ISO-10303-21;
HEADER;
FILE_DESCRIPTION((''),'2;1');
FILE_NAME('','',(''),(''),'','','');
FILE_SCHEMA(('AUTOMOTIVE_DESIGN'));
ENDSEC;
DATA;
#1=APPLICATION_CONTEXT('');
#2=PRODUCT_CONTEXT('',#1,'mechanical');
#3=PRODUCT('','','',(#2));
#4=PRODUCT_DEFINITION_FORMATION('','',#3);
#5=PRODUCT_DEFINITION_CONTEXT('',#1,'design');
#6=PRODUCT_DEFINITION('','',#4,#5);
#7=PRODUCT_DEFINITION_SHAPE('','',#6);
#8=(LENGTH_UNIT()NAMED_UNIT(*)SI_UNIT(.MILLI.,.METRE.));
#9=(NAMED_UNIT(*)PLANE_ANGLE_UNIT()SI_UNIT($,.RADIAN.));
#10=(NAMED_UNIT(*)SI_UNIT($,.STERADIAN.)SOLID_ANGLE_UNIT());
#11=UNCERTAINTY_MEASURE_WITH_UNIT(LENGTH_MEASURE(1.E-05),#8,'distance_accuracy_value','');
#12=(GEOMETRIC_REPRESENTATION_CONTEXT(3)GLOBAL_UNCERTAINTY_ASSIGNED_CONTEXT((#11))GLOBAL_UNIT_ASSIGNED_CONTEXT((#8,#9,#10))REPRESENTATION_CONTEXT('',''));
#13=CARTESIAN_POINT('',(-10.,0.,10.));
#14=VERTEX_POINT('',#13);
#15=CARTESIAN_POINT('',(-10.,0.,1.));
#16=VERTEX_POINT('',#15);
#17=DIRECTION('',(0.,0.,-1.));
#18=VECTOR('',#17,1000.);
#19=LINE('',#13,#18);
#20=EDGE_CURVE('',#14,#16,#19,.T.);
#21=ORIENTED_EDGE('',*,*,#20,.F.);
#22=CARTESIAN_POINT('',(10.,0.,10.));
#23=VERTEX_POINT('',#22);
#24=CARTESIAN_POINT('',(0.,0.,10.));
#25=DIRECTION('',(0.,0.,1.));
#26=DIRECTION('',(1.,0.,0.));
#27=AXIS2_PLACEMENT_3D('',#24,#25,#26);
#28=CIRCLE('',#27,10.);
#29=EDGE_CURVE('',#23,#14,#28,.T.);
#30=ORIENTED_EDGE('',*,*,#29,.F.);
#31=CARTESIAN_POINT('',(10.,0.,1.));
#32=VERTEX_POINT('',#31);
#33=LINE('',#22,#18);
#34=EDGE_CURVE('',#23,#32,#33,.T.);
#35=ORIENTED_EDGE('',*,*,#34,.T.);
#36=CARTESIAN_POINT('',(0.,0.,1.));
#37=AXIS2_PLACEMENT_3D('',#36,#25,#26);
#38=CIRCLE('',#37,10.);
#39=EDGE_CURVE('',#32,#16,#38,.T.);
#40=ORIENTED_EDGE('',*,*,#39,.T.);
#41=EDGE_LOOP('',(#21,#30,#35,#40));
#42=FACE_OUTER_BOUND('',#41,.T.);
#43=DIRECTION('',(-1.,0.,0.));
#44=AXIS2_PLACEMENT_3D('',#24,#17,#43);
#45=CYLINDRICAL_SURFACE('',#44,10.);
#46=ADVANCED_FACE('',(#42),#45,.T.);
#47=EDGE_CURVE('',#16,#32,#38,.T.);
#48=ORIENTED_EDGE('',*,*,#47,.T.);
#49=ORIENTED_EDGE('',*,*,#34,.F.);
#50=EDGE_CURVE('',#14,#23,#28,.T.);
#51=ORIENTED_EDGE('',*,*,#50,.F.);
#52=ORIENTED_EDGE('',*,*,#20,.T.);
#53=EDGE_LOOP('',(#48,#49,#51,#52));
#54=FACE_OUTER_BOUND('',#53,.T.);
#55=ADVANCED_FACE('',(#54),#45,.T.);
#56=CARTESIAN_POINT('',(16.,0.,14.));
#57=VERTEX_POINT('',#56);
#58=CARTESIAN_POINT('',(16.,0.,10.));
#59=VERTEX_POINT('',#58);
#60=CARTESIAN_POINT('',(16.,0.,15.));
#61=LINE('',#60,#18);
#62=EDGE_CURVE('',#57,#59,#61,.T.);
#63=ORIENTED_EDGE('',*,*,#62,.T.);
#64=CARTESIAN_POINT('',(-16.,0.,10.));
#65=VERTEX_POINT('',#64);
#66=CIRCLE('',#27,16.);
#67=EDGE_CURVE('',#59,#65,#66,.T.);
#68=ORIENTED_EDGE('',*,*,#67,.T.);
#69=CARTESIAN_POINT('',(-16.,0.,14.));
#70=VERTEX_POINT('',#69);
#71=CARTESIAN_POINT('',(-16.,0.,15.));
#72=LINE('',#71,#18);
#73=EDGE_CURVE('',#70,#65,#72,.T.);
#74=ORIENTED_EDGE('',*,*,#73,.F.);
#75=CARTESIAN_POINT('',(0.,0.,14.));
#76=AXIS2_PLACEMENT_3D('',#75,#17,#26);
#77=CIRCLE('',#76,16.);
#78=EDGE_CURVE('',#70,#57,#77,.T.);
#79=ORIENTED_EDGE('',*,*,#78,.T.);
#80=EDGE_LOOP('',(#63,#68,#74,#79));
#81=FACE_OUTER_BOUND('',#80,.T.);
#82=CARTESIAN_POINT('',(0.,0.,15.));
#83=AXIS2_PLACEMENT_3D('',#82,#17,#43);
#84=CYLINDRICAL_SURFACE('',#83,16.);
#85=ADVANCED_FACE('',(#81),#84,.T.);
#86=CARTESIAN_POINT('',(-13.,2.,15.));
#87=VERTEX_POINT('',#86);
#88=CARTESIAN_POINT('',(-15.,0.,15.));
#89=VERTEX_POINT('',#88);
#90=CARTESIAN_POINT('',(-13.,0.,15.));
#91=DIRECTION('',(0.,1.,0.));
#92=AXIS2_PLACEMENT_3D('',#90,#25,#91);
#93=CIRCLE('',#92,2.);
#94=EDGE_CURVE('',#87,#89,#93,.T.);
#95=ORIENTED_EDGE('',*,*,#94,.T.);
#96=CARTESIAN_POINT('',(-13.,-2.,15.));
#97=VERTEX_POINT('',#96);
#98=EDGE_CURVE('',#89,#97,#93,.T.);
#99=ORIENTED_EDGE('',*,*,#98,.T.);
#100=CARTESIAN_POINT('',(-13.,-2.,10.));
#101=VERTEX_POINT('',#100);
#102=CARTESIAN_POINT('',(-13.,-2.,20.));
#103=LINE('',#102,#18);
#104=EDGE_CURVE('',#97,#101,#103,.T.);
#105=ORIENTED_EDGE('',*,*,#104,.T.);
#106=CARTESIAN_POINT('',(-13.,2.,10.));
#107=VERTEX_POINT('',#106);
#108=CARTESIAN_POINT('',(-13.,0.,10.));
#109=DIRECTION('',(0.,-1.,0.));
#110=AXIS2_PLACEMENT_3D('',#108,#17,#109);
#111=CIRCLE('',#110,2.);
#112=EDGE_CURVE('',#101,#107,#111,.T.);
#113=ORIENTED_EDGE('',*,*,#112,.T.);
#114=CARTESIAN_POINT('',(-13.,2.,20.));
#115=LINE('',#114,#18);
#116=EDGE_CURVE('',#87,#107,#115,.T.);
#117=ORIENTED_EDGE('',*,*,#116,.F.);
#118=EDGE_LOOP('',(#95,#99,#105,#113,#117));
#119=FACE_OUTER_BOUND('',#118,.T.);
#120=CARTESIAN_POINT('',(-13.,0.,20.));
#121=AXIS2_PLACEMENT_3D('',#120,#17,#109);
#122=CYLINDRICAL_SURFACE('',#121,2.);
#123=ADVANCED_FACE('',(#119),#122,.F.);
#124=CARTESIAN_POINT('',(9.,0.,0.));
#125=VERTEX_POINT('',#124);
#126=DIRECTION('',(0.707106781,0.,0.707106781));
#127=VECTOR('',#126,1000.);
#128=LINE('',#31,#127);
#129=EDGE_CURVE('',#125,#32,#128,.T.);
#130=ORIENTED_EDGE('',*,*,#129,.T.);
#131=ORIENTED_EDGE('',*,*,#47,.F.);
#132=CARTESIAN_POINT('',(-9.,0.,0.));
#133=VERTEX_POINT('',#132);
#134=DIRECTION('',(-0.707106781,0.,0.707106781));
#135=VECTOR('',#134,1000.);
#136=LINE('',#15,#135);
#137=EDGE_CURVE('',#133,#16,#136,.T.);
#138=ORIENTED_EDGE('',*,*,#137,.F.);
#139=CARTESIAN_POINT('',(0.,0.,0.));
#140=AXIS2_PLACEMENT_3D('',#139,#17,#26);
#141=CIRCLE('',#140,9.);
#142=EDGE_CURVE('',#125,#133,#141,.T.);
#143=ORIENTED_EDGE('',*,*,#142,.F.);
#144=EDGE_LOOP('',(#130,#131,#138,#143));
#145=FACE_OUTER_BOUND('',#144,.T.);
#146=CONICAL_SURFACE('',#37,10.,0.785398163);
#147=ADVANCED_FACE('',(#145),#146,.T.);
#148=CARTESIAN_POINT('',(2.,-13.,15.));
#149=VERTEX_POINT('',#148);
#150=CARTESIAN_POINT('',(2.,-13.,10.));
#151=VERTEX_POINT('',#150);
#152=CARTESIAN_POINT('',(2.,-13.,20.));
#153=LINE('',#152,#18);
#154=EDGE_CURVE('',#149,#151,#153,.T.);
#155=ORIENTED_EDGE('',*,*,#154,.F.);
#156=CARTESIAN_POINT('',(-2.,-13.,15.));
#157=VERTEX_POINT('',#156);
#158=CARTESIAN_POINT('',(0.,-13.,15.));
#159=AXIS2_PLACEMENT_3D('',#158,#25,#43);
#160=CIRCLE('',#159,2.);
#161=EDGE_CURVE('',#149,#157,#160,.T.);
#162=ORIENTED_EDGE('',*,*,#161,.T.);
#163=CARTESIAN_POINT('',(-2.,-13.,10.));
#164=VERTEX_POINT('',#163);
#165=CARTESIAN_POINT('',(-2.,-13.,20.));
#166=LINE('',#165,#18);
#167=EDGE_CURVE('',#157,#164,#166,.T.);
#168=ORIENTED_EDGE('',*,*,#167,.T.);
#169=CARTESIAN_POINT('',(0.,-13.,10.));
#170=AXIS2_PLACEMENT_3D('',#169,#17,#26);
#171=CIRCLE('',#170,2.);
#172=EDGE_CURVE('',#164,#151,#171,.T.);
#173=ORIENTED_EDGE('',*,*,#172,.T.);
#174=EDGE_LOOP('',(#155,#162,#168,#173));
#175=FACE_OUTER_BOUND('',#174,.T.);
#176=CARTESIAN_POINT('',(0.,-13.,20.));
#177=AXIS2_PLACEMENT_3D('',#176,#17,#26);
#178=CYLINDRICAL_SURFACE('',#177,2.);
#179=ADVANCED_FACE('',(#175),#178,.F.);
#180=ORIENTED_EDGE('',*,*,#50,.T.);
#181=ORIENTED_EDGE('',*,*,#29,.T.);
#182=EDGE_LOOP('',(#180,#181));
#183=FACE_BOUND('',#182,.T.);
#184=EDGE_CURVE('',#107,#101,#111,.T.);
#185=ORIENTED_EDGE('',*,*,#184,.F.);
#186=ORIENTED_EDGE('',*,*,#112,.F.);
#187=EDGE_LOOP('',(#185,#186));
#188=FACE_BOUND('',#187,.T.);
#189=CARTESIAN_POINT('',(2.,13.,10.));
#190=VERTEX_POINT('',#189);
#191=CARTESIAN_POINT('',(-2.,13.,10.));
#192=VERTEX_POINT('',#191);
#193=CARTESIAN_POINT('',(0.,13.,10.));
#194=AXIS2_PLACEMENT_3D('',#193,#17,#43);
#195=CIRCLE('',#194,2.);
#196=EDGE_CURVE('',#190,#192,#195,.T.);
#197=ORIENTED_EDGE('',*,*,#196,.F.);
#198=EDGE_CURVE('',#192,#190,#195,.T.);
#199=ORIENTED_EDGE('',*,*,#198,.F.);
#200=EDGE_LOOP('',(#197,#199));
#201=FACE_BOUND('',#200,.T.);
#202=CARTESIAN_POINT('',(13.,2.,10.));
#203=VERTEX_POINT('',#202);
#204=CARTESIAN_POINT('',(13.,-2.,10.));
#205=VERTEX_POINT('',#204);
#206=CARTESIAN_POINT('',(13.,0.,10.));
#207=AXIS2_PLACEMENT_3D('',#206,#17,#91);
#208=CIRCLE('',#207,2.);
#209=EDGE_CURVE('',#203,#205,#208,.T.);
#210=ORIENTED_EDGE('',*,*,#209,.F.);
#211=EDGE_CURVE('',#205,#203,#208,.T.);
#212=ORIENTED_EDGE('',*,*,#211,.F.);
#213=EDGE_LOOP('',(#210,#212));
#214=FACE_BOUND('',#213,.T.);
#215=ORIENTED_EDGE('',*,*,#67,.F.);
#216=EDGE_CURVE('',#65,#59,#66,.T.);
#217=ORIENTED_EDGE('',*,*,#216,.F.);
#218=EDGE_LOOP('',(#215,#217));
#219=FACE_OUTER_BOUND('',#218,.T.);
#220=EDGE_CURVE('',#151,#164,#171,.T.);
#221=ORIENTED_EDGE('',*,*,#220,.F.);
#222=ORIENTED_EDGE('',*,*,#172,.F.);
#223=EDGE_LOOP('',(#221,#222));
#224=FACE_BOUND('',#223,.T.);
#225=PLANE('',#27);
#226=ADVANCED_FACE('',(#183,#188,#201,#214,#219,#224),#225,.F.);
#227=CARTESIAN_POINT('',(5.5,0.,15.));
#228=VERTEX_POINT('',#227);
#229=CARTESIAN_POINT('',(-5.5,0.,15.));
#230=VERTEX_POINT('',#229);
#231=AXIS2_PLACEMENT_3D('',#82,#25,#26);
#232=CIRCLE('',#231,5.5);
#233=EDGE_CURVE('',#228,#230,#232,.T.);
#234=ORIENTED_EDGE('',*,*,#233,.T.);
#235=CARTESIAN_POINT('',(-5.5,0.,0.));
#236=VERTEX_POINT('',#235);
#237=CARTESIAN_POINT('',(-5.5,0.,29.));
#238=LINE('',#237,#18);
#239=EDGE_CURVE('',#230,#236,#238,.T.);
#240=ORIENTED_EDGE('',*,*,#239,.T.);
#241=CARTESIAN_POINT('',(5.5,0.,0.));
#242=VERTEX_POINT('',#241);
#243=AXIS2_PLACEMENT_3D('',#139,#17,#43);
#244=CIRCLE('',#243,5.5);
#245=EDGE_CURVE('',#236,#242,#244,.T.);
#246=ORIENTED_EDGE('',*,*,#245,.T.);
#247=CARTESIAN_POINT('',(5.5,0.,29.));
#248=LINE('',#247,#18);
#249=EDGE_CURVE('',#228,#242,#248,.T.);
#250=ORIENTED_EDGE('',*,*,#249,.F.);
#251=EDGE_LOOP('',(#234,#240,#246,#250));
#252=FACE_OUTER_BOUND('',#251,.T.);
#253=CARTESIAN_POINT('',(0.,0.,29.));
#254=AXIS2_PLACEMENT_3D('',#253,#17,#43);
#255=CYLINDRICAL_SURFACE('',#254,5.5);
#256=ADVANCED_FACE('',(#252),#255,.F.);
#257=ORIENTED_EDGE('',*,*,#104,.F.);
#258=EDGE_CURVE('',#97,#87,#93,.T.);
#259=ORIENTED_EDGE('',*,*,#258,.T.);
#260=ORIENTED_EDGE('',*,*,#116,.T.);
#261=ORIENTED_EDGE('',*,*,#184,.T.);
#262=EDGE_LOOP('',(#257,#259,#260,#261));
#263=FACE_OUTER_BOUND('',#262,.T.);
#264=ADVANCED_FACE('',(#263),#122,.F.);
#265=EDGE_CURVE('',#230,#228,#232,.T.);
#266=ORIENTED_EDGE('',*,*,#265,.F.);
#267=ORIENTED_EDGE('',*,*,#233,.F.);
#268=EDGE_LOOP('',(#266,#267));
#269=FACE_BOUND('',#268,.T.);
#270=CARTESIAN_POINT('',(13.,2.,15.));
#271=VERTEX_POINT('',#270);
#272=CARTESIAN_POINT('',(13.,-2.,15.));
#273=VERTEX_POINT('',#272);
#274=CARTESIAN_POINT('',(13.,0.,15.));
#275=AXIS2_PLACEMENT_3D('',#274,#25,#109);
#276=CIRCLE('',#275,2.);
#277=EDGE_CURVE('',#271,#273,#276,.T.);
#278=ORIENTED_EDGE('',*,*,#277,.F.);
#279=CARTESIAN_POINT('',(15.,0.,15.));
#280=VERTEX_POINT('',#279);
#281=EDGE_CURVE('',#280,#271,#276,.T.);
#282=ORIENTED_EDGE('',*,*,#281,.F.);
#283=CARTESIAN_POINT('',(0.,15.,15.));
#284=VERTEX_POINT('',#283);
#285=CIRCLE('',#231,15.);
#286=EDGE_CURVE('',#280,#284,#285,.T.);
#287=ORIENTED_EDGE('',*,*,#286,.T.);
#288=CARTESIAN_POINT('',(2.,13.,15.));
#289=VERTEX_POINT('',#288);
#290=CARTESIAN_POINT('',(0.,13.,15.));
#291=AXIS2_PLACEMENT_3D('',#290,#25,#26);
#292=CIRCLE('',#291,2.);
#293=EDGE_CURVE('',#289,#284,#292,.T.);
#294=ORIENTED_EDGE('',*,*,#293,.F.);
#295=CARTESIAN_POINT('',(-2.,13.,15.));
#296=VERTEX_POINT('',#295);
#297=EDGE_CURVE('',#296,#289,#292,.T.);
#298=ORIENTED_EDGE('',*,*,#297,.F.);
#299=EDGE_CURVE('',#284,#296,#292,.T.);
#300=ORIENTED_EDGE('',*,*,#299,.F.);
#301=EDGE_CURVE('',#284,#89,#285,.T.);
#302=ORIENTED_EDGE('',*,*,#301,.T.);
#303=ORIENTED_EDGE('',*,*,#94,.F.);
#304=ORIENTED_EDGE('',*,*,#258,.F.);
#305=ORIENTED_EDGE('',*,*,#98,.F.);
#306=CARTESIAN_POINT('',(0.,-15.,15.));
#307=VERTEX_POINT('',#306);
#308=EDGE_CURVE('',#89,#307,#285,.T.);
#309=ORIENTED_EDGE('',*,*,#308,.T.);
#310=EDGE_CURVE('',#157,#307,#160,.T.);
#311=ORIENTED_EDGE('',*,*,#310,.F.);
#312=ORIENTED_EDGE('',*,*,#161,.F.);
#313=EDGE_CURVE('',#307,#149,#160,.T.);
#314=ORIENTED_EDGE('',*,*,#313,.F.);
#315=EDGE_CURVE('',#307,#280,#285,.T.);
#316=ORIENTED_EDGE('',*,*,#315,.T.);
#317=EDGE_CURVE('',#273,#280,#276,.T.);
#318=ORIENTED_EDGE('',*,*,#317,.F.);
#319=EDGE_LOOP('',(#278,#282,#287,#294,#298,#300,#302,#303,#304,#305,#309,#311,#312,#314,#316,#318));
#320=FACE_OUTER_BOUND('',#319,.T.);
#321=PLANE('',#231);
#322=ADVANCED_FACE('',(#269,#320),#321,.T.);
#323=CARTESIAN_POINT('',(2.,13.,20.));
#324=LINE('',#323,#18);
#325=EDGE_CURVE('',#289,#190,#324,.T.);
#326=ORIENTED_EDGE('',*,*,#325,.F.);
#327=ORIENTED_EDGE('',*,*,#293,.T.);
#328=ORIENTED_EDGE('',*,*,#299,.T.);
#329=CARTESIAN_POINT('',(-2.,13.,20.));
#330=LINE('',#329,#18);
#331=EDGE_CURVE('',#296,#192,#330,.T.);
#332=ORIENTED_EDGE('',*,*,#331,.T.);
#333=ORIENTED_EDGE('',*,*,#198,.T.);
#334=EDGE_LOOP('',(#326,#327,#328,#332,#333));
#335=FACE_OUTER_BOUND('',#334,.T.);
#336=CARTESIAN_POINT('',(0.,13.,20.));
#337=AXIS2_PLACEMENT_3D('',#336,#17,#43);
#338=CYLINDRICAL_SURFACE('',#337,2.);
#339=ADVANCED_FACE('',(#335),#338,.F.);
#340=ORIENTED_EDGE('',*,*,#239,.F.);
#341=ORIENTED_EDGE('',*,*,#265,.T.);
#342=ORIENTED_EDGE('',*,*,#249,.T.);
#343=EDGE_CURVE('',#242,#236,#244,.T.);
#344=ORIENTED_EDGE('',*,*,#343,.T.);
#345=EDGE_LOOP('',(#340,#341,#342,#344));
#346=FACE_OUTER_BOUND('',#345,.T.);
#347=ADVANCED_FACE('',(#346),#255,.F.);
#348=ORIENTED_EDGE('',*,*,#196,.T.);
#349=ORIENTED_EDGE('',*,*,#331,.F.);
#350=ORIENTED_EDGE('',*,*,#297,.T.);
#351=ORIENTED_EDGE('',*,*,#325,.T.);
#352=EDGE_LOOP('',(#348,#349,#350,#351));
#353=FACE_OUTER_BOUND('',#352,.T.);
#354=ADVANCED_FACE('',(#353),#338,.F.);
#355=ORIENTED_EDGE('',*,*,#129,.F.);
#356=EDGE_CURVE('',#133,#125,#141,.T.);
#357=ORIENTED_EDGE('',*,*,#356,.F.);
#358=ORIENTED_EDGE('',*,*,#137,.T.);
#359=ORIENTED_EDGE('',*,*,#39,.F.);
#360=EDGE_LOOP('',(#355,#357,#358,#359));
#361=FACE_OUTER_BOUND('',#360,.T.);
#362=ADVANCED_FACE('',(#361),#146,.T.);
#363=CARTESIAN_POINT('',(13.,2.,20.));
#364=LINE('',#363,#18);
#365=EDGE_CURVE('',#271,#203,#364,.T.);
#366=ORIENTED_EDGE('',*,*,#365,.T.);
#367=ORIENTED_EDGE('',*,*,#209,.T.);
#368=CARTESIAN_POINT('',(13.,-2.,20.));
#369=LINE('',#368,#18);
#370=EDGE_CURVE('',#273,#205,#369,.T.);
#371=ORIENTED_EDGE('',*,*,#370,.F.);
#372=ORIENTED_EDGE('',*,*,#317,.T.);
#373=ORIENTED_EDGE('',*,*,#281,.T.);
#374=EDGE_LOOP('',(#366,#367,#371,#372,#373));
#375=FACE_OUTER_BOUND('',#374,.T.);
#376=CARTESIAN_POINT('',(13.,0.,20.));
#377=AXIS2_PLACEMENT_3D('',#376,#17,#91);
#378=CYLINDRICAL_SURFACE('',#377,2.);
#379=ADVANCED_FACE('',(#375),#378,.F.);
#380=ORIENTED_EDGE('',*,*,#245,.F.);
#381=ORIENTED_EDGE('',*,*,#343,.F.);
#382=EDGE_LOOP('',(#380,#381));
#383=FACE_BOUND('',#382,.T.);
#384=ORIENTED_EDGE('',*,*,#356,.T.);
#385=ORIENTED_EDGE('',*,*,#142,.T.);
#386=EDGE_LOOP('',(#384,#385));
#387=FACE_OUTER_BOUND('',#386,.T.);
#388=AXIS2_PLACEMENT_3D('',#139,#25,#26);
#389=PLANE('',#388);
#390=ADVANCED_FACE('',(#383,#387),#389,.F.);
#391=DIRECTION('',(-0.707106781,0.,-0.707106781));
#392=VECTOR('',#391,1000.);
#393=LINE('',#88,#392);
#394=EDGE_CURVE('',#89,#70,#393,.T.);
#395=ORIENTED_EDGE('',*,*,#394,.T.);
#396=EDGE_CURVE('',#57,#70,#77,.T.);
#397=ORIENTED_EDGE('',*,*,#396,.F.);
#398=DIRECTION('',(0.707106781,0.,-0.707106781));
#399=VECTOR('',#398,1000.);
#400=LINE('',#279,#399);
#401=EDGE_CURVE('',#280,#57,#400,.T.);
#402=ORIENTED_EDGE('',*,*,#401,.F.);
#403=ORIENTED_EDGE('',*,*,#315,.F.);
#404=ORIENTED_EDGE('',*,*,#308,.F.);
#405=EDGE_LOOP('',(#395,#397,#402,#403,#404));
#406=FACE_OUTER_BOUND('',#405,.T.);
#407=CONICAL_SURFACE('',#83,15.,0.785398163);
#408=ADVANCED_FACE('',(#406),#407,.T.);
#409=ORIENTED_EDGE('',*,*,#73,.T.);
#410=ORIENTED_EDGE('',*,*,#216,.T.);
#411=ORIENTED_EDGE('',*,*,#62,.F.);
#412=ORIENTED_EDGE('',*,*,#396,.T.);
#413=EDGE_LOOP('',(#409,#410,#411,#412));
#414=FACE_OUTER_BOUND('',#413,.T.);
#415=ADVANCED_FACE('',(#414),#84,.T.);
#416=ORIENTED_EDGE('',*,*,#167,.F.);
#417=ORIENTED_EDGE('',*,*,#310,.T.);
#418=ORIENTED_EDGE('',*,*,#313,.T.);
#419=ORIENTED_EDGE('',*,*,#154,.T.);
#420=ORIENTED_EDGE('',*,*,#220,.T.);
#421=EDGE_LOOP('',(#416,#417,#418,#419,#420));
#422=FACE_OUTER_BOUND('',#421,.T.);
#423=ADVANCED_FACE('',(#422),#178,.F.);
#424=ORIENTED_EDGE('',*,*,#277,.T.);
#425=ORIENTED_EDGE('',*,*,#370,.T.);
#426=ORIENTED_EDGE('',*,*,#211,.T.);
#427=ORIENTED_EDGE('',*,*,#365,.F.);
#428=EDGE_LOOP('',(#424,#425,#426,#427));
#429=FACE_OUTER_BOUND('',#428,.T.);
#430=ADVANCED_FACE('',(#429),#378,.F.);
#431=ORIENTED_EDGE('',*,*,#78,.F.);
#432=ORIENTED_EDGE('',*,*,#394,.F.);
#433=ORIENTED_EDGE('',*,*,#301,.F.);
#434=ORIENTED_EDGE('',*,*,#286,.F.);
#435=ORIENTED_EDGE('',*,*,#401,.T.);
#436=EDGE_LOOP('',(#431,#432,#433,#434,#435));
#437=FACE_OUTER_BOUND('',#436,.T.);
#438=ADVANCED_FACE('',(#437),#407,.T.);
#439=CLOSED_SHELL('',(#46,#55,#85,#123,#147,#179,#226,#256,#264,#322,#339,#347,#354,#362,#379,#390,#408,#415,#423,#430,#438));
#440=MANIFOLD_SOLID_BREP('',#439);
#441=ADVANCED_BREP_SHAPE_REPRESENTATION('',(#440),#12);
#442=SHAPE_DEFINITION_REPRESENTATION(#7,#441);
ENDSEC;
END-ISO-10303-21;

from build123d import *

# Parameters (mm, degrees)
SKETCH1_R           = 10
BOSS_EXTRUDE1_DEPTH = 10
SKETCH2_R           = 16
BOSS_EXTRUDE2_DEPTH = 5
CHAMFER1_SIZE       = 1
SKETCH3_R           = 2
CUT_EXTRUDE1_DEPTH  = 10
CIRPATTERN1_COUNT   = 4
SKETCH4_R           = 5.5
CUT_EXTRUDE2_DEPTH  = 29


with BuildPart() as part:
    # Sketch1 → Boss-Extrude1 (new body)
    with BuildSketch(Plane.XY):
        Circle(SKETCH1_R)
    extrude(amount=BOSS_EXTRUDE1_DEPTH)

    # Sketch2 → Boss-Extrude2 (add)
    with BuildSketch(Plane.XY.offset(10)):
        Circle(SKETCH2_R)
    extrude(amount=BOSS_EXTRUDE2_DEPTH)

    # Chamfer1
    chamfer1_edges = [part.edges().sort_by_distance(p)[0] for p in [
        (-10, 0, 0),
        (-16, 0, 15),
    ]]
    chamfer(chamfer1_edges, length=CHAMFER1_SIZE)

    # Sketch3 → Cut-Extrude1 (cut)
    with BuildSketch(Plane(origin=(0, 0, 10), x_dir=(-1, 0, 0), z_dir=(0, 0, -1))):
        with Locations((0, 13)):
            Circle(SKETCH3_R)
    cut_extrude1 = extrude(amount=-CUT_EXTRUDE1_DEPTH, mode=Mode.SUBTRACT)

    # CirPattern1: Cut-Extrude1 ×4 about axis
    cirpattern1_axis = Axis((0, 0, 0), (0, 0, 1))
    for i in range(1, CIRPATTERN1_COUNT):
        add(cut_extrude1.rotate(cirpattern1_axis, i * 360 / CIRPATTERN1_COUNT), mode=Mode.SUBTRACT)

    # Sketch4 → Cut-Extrude2 (cut)
    with BuildSketch(Plane(origin=(0, 0, 0), x_dir=(-1, 0, 0), z_dir=(0, 0, -1))):
        Circle(SKETCH4_R)
    extrude(amount=-CUT_EXTRUDE2_DEPTH, mode=Mode.SUBTRACT)


solid = part.part
